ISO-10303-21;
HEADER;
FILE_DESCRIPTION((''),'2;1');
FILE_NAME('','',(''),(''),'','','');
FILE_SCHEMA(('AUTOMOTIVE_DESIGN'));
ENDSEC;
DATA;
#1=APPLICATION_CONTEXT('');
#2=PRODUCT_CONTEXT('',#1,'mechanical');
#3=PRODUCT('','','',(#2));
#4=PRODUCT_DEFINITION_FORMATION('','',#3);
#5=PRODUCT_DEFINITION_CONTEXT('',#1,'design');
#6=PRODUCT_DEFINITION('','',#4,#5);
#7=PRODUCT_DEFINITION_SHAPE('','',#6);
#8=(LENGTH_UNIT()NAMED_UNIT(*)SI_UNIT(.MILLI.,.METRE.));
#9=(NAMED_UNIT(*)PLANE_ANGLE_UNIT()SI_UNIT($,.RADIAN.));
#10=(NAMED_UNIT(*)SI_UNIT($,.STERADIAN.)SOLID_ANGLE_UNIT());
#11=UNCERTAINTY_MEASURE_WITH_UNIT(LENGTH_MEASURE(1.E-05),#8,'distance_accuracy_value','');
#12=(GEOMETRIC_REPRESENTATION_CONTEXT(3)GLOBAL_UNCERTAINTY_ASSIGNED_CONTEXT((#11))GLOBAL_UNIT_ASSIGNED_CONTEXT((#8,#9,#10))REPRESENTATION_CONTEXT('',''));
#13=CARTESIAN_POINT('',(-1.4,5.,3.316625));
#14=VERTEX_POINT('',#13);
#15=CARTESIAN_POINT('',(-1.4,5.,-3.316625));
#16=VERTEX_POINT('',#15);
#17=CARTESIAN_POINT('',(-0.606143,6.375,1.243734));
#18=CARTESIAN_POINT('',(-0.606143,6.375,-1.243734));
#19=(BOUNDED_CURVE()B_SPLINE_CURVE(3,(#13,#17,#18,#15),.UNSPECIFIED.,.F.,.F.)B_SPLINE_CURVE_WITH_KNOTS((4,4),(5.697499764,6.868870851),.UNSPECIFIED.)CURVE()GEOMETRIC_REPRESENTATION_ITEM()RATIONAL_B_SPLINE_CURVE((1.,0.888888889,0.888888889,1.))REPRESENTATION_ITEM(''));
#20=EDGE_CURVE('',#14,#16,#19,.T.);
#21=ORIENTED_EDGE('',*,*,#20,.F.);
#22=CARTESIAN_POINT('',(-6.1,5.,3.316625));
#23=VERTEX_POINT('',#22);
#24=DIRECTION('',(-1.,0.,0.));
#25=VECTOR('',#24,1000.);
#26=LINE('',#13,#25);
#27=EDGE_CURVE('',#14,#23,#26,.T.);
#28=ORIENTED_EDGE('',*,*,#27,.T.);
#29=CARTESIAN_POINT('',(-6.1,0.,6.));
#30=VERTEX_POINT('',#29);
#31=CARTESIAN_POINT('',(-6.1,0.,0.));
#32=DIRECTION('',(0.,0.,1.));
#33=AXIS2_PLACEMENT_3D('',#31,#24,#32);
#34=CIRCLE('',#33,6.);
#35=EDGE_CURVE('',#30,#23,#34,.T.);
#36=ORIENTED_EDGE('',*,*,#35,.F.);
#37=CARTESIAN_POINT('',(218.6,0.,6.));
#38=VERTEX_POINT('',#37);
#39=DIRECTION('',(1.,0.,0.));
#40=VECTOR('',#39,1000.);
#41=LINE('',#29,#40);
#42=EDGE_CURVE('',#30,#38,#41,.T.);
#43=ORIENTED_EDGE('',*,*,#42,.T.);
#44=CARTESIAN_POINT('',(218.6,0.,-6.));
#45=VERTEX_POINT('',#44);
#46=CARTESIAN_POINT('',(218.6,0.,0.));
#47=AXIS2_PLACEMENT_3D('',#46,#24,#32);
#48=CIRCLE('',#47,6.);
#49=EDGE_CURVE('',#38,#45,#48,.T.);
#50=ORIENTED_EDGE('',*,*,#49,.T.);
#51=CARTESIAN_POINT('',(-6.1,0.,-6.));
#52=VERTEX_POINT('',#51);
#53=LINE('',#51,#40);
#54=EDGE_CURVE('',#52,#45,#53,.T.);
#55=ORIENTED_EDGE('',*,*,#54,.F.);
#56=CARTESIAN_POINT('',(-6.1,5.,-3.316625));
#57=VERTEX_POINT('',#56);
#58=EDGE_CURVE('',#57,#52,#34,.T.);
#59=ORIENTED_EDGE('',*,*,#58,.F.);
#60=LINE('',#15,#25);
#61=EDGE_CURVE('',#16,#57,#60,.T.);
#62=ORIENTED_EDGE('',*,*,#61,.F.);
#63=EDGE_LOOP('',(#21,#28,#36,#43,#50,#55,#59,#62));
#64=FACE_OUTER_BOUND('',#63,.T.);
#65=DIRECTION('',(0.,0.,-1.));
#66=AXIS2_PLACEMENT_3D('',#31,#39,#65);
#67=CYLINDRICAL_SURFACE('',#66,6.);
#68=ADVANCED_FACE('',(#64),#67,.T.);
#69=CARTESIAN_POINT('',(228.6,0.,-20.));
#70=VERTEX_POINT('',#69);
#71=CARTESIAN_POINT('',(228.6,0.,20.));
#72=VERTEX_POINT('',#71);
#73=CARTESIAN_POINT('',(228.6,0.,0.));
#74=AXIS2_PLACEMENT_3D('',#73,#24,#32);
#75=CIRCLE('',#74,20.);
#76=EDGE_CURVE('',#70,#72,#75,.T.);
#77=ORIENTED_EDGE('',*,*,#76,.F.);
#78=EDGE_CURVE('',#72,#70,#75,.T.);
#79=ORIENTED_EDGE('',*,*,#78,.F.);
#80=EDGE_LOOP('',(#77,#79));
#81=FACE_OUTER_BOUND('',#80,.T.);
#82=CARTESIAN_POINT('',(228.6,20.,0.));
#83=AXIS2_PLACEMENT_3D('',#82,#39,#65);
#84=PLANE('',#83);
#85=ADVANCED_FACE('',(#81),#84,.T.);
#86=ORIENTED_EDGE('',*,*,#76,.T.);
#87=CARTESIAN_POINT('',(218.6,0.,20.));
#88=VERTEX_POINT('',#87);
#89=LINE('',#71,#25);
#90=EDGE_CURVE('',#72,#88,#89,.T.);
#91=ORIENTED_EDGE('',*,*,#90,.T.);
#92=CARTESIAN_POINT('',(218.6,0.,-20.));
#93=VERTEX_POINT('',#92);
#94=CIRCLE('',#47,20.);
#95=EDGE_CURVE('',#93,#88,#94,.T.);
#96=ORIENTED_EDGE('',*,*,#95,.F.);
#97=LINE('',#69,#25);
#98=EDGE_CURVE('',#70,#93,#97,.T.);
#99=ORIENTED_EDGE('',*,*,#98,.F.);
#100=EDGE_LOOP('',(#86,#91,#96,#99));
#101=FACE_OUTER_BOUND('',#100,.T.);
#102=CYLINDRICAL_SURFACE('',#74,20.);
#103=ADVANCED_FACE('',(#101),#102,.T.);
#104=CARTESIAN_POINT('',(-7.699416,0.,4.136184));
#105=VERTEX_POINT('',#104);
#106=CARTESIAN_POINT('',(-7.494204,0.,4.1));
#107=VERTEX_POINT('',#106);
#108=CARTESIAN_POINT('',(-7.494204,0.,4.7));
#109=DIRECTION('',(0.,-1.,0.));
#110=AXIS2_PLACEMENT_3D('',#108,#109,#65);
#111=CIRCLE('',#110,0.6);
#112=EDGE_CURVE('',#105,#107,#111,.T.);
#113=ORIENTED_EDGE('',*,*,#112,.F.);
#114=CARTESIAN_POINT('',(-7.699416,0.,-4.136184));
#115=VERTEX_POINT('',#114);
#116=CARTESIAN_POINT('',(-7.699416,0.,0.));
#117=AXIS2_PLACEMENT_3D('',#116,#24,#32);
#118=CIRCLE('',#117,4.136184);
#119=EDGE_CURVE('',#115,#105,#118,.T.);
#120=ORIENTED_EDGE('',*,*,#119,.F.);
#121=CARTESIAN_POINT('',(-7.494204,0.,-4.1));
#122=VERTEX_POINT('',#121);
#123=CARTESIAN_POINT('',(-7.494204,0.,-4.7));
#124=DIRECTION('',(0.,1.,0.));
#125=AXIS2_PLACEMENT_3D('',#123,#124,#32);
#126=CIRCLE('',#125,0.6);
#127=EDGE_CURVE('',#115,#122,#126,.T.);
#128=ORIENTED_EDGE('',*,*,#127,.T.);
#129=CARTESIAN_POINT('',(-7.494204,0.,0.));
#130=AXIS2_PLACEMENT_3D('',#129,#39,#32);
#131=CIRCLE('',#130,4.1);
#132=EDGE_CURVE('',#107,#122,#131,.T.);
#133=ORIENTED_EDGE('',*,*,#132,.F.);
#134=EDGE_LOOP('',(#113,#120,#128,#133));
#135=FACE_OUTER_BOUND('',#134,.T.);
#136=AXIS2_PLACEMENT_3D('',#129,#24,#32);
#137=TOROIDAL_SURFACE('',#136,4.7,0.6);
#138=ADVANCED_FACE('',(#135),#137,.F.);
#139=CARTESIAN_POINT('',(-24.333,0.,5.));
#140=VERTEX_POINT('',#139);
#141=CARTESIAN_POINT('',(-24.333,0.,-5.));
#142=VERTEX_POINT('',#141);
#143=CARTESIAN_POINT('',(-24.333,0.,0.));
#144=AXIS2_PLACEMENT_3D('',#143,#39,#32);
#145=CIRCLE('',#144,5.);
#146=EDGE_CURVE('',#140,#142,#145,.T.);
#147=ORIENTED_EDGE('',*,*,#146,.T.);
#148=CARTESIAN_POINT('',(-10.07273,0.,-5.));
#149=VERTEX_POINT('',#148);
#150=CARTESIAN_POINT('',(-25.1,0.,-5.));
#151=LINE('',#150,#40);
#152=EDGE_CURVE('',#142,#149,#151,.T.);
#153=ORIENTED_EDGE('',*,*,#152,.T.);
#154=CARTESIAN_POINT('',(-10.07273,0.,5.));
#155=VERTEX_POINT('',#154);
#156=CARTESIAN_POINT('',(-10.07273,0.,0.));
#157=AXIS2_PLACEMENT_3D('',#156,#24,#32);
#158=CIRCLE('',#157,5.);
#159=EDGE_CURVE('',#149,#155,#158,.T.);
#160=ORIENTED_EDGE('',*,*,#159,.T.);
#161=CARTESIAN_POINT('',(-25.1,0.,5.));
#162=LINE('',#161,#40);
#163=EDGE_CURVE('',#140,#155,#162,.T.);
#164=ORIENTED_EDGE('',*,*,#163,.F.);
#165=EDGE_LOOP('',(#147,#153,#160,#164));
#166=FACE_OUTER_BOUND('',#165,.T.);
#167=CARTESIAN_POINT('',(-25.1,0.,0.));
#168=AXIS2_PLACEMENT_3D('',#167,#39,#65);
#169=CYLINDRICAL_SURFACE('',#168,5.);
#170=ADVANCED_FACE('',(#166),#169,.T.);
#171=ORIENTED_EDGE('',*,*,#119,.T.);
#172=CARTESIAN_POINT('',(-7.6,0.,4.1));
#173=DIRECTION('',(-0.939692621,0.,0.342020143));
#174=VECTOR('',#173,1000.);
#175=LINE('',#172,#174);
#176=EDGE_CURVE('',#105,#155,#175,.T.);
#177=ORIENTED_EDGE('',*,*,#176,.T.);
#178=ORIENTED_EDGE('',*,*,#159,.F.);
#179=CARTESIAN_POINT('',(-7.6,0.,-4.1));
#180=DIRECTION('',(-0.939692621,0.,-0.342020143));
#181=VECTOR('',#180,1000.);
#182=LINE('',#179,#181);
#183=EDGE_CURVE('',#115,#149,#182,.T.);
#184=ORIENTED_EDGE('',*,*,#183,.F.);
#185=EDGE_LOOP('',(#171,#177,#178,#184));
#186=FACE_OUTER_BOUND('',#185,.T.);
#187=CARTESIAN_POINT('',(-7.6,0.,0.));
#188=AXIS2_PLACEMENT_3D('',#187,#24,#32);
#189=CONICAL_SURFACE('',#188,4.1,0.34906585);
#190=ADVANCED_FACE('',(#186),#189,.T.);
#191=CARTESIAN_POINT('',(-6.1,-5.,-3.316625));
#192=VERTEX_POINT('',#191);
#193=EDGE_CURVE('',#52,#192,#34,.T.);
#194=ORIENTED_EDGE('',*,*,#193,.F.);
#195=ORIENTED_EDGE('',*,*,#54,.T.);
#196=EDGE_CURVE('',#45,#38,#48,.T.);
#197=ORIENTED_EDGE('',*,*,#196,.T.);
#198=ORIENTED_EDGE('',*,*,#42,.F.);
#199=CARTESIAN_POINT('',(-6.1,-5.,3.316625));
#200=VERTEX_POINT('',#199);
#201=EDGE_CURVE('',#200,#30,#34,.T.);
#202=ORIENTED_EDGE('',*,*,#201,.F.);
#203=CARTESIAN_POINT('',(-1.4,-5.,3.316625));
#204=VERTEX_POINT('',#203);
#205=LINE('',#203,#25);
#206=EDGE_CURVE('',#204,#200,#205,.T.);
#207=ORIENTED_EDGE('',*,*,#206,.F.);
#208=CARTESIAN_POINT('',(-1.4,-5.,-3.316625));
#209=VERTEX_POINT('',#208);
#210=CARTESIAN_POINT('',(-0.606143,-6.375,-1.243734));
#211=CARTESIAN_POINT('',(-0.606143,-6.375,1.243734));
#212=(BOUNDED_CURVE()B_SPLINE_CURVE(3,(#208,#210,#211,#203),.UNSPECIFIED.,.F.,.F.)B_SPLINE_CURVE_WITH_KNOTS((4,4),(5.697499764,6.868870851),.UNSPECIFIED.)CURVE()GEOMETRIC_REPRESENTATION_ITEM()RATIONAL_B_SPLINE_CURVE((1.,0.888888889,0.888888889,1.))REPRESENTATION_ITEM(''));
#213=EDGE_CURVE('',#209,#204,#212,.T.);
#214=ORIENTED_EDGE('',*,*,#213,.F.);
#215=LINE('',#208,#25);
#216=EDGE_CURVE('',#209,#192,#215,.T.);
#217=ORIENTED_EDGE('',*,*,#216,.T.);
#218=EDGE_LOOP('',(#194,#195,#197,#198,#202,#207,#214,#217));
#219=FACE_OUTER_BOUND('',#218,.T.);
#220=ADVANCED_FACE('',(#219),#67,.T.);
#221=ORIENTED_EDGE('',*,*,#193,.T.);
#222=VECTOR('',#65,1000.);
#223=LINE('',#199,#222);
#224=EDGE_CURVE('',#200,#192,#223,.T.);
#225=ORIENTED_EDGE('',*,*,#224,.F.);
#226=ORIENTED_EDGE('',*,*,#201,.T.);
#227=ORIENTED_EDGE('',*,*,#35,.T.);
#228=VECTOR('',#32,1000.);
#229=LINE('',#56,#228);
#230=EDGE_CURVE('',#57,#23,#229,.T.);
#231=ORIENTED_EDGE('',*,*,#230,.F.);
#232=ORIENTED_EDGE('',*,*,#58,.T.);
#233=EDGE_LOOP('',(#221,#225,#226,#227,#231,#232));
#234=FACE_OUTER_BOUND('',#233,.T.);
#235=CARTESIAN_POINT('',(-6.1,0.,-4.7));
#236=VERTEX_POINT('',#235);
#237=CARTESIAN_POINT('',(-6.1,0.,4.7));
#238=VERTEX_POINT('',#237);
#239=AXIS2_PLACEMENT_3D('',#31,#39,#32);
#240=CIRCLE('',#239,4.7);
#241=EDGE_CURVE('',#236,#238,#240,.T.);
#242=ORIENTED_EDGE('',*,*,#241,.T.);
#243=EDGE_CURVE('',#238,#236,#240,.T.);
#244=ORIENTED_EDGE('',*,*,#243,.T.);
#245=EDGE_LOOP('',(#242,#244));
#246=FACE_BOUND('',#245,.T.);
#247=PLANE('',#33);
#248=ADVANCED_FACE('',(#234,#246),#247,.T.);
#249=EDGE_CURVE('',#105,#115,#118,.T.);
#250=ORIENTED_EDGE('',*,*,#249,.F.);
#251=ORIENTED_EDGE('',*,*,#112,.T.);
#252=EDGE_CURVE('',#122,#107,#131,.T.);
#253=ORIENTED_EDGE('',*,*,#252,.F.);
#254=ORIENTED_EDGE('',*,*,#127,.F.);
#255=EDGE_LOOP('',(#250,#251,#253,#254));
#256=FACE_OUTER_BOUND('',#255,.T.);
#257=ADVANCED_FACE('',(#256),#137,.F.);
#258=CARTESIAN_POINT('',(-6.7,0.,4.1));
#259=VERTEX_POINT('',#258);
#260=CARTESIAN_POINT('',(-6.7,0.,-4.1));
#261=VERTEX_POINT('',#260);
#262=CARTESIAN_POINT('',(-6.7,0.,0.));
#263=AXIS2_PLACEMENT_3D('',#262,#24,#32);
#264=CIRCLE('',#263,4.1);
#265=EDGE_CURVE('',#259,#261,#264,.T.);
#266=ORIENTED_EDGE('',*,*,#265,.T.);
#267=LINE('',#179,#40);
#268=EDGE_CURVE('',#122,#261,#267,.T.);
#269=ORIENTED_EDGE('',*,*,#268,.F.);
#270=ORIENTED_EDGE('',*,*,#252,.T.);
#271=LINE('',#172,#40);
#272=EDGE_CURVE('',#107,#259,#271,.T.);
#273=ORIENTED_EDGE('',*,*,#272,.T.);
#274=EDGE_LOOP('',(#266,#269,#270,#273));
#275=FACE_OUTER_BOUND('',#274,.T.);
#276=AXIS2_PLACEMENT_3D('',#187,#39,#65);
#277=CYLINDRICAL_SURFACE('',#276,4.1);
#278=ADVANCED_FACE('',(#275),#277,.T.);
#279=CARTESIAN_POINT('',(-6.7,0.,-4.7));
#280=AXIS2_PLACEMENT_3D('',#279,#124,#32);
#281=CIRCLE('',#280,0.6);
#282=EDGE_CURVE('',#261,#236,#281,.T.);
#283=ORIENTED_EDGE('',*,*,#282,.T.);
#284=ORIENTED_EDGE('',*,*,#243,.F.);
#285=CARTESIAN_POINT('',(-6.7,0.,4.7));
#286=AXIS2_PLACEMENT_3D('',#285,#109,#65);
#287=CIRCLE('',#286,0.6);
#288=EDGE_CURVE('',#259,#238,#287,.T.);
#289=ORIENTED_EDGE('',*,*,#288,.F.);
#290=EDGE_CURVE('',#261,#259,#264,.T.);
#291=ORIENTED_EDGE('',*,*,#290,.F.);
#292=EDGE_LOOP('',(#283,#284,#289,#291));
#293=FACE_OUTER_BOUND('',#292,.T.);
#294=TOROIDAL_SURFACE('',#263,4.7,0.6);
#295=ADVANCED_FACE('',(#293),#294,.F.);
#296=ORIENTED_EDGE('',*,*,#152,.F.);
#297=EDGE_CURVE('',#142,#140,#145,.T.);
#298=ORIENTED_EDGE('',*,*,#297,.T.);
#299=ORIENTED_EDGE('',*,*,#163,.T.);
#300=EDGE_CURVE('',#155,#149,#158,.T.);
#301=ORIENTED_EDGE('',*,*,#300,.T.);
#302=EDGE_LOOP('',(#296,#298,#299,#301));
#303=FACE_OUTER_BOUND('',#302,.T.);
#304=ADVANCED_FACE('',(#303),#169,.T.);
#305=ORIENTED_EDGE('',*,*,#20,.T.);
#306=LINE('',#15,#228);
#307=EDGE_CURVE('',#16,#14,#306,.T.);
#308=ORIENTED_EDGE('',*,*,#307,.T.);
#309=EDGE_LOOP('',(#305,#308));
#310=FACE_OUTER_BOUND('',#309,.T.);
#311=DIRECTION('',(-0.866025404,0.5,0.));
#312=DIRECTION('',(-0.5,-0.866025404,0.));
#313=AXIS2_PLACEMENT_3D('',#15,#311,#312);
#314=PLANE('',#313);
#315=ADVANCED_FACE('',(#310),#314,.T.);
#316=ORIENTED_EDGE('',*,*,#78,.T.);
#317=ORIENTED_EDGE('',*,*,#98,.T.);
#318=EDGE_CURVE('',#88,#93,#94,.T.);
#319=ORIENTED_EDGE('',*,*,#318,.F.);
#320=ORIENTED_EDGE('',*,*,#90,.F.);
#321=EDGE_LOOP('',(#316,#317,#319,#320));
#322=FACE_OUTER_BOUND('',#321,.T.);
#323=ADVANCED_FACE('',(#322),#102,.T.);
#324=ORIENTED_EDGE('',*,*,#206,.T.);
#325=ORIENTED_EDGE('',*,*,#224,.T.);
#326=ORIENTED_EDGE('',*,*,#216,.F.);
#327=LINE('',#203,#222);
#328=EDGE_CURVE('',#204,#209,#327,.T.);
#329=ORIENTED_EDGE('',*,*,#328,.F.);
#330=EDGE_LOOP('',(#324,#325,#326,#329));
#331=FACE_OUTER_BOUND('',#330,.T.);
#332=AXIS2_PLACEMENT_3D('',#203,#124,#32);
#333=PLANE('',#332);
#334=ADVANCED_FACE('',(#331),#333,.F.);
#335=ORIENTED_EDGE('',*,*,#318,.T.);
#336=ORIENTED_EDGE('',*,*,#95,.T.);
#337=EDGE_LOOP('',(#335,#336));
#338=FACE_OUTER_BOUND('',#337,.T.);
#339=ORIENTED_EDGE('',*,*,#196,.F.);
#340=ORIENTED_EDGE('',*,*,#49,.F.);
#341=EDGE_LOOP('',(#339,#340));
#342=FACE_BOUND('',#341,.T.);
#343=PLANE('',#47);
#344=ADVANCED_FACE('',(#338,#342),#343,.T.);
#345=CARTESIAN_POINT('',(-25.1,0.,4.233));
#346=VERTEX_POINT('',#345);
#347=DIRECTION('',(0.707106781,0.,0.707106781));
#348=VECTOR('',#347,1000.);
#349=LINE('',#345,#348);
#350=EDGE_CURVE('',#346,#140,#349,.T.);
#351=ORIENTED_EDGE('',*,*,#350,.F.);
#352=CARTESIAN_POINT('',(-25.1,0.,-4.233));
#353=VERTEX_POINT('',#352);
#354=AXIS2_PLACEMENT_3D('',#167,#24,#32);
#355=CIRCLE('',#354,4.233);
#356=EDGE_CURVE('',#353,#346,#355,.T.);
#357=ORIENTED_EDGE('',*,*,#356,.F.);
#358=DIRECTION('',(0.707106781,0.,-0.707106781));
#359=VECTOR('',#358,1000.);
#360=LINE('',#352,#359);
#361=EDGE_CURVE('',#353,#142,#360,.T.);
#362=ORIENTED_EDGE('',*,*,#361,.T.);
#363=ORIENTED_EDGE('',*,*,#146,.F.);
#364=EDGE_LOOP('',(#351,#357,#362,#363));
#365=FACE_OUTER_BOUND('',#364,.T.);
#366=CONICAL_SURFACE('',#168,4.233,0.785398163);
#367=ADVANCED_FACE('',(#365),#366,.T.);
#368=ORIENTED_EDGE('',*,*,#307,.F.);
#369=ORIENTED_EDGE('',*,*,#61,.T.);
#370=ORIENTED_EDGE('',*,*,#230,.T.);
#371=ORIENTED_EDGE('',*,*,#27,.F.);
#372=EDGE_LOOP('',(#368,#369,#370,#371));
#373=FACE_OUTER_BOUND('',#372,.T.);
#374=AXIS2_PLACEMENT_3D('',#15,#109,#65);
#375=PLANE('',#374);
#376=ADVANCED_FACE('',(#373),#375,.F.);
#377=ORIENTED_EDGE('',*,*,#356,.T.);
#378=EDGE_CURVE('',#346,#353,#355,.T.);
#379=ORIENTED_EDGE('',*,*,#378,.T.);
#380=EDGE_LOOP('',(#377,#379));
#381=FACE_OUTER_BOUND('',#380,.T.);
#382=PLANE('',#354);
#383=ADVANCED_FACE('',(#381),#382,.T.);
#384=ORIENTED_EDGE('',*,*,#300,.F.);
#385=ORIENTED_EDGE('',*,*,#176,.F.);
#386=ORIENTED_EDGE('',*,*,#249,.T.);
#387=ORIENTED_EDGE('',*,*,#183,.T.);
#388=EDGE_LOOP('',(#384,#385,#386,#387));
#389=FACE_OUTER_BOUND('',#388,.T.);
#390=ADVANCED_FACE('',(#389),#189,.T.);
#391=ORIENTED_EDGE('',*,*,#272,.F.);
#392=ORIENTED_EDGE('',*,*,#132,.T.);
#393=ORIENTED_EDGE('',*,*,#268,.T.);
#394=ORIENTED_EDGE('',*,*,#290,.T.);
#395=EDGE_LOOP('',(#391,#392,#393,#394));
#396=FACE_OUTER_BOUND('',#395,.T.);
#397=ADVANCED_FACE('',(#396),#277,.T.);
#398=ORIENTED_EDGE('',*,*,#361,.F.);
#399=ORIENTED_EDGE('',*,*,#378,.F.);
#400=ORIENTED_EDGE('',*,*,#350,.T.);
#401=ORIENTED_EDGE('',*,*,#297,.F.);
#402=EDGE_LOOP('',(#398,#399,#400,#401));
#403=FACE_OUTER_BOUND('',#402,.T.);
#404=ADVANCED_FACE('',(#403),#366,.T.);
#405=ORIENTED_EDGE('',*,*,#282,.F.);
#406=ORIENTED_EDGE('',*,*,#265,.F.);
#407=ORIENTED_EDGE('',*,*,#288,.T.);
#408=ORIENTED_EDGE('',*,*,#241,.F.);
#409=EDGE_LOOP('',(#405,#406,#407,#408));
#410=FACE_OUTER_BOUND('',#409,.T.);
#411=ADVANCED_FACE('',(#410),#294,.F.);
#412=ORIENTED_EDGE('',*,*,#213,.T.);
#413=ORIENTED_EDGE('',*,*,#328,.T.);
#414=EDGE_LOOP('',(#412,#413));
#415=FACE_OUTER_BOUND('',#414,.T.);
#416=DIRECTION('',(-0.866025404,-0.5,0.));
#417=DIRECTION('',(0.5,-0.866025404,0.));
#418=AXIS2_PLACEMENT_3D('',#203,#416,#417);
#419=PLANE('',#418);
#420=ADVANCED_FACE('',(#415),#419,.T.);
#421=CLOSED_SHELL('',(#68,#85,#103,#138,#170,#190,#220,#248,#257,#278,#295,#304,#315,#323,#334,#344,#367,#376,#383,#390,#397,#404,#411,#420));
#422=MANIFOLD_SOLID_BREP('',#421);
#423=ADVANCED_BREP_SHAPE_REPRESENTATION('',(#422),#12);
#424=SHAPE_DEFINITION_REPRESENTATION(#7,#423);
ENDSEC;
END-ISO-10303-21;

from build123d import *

# Parameters (mm, degrees)
SKETCH_1_W          = 10
SKETCH_1_H          = 20
SKETCH_2_R          = 6
EXTRUDE_1_DEPTH     = 224.7
CUT_EXTRUDE_START   = -4.7
CUT_EXTRUDE_1_DEPTH = 4.7
CUT_EXTRUDE_2_DEPTH = 4.7
SKETCH_5_R          = 4.1
EXTRUDE_2_DEPTH     = 1.5
SKETCH_6_R          = 4.1
EXTRUDE_3_DEPTH     = 2.472729678
EXTRUDE_3_DRAFT     = -20
SKETCH_7_R          = 5
EXTRUDE_4_DEPTH     = 15.027270322
DRAFT_1_ANGLE       = 30
DRAFT_2_ANGLE       = 30
CHAMFER_1_SIZE      = 0.767
FILLET_1_R          = 0.6


with BuildPart() as part:
    # 草图1 → 旋转1 (revolve)
    with BuildSketch(Plane(origin=(0, 0, 0), x_dir=(-1, 0, 0), z_dir=(0, 0, -1)), mode=Mode.PRIVATE) as revolve_1_sk:
        with Locations((-223.6, 10)):
            Rectangle(SKETCH_1_W, SKETCH_1_H)
    revolve(revolve_1_sk.sketch.rotate(Axis((228.6, 0, 0), (-1, 0, 0)), 270), axis=Axis((228.6, 0, 0), (-1, 0, 0)))

    # 草图2 → 凸台-拉伸1 (add)
    with BuildSketch(Plane.ZY.offset(-218.6)):
        Circle(SKETCH_2_R)
    extrude(amount=EXTRUDE_1_DEPTH)

    # 草图3 → 切除-拉伸1 (cut)
    with BuildSketch(Plane.ZY.offset(6.1).offset(CUT_EXTRUDE_START)):
        with BuildLine():
            Line((-3.31662479, 5), (3.31662479, 5))
            ThreePointArc((3.31662479, 5), (0, 6), (-3.31662479, 5))
        make_face()
    extrude(amount=CUT_EXTRUDE_1_DEPTH, mode=Mode.SUBTRACT)

    # 草图4 → 切除-拉伸2 (cut)
    with BuildSketch(Plane.ZY.offset(6.1).offset(CUT_EXTRUDE_START)):
        with BuildLine():
            Line((3.31662479, -5), (-3.31662479, -5))
            ThreePointArc((-3.31662479, -5), (0, -6), (3.31662479, -5))
        make_face()
    extrude(amount=CUT_EXTRUDE_2_DEPTH, mode=Mode.SUBTRACT)

    # 草图5 → 凸台-拉伸2 (add)
    with BuildSketch(Plane.ZY.offset(6.1)):
        Circle(SKETCH_5_R)
    extrude(amount=EXTRUDE_2_DEPTH)


with BuildPart() as extrude_3_tool:
    # 草图6 → 凸台-拉伸3 (with draft: the straight prism first)
    with BuildSketch(Plane.ZY.offset(7.6)):
        Circle(SKETCH_6_R)
    extrude(amount=EXTRUDE_3_DEPTH)
    # 凸台-拉伸3: the draft: its side faces are tilted about the plane it starts from
    extrude_3_sides = [extrude_3_tool.faces().sort_by_distance(p)[0] for p in [
        (-8.836364839, 0, -4.1),
    ]]
    draft(extrude_3_sides, Plane.ZY.offset(7.6), EXTRUDE_3_DRAFT)


with BuildPart() as part_1:
    add(part.part)

    # 凸台-拉伸3: add extrude_3_tool
    add(extrude_3_tool.part)

    # 草图7 → 凸台-拉伸4 (add)
    with BuildSketch(Plane.ZY.offset(10.072729678)):
        with Locations(Location((0, 0, 0), (0, 0, 180))):
            Circle(SKETCH_7_R)
    extrude(amount=EXTRUDE_4_DEPTH)

    # 拔模1
    draft_1_faces = [part_1.faces().sort_by_distance(p)[0] for p in [
        (-1.4, -5.403002256, 0),
    ]]
    draft(draft_1_faces, Plane(origin=(-1.4, -5, 3.31662479), x_dir=(0, 0, -1), z_dir=(0, -1, 0)), DRAFT_1_ANGLE)

    # 拔模2
    draft_2_faces = [part_1.faces().sort_by_distance(p)[0] for p in [
        (-1.4, 5.403002256, 0),
    ]]
    draft(draft_2_faces, Plane(origin=(-1.4, 5, -3.31662479), x_dir=(0, 0, 1), z_dir=(0, 1, 0)), DRAFT_2_ANGLE)

    # 倒角1
    chamfer_1_edges = [part_1.edges().sort_by_distance(p)[0] for p in [
        (-25.1, 0, 5),
    ]]
    chamfer(chamfer_1_edges, length=CHAMFER_1_SIZE)

    # 圆角1
    fillet_1_edges = [part_1.edges().sort_by_distance(p)[0] for p in [
        (-6.1, 0, -4.1),
        (-7.6, 0, -4.1),
    ]]
    fillet(fillet_1_edges, radius=FILLET_1_R)


solid = part_1.part
